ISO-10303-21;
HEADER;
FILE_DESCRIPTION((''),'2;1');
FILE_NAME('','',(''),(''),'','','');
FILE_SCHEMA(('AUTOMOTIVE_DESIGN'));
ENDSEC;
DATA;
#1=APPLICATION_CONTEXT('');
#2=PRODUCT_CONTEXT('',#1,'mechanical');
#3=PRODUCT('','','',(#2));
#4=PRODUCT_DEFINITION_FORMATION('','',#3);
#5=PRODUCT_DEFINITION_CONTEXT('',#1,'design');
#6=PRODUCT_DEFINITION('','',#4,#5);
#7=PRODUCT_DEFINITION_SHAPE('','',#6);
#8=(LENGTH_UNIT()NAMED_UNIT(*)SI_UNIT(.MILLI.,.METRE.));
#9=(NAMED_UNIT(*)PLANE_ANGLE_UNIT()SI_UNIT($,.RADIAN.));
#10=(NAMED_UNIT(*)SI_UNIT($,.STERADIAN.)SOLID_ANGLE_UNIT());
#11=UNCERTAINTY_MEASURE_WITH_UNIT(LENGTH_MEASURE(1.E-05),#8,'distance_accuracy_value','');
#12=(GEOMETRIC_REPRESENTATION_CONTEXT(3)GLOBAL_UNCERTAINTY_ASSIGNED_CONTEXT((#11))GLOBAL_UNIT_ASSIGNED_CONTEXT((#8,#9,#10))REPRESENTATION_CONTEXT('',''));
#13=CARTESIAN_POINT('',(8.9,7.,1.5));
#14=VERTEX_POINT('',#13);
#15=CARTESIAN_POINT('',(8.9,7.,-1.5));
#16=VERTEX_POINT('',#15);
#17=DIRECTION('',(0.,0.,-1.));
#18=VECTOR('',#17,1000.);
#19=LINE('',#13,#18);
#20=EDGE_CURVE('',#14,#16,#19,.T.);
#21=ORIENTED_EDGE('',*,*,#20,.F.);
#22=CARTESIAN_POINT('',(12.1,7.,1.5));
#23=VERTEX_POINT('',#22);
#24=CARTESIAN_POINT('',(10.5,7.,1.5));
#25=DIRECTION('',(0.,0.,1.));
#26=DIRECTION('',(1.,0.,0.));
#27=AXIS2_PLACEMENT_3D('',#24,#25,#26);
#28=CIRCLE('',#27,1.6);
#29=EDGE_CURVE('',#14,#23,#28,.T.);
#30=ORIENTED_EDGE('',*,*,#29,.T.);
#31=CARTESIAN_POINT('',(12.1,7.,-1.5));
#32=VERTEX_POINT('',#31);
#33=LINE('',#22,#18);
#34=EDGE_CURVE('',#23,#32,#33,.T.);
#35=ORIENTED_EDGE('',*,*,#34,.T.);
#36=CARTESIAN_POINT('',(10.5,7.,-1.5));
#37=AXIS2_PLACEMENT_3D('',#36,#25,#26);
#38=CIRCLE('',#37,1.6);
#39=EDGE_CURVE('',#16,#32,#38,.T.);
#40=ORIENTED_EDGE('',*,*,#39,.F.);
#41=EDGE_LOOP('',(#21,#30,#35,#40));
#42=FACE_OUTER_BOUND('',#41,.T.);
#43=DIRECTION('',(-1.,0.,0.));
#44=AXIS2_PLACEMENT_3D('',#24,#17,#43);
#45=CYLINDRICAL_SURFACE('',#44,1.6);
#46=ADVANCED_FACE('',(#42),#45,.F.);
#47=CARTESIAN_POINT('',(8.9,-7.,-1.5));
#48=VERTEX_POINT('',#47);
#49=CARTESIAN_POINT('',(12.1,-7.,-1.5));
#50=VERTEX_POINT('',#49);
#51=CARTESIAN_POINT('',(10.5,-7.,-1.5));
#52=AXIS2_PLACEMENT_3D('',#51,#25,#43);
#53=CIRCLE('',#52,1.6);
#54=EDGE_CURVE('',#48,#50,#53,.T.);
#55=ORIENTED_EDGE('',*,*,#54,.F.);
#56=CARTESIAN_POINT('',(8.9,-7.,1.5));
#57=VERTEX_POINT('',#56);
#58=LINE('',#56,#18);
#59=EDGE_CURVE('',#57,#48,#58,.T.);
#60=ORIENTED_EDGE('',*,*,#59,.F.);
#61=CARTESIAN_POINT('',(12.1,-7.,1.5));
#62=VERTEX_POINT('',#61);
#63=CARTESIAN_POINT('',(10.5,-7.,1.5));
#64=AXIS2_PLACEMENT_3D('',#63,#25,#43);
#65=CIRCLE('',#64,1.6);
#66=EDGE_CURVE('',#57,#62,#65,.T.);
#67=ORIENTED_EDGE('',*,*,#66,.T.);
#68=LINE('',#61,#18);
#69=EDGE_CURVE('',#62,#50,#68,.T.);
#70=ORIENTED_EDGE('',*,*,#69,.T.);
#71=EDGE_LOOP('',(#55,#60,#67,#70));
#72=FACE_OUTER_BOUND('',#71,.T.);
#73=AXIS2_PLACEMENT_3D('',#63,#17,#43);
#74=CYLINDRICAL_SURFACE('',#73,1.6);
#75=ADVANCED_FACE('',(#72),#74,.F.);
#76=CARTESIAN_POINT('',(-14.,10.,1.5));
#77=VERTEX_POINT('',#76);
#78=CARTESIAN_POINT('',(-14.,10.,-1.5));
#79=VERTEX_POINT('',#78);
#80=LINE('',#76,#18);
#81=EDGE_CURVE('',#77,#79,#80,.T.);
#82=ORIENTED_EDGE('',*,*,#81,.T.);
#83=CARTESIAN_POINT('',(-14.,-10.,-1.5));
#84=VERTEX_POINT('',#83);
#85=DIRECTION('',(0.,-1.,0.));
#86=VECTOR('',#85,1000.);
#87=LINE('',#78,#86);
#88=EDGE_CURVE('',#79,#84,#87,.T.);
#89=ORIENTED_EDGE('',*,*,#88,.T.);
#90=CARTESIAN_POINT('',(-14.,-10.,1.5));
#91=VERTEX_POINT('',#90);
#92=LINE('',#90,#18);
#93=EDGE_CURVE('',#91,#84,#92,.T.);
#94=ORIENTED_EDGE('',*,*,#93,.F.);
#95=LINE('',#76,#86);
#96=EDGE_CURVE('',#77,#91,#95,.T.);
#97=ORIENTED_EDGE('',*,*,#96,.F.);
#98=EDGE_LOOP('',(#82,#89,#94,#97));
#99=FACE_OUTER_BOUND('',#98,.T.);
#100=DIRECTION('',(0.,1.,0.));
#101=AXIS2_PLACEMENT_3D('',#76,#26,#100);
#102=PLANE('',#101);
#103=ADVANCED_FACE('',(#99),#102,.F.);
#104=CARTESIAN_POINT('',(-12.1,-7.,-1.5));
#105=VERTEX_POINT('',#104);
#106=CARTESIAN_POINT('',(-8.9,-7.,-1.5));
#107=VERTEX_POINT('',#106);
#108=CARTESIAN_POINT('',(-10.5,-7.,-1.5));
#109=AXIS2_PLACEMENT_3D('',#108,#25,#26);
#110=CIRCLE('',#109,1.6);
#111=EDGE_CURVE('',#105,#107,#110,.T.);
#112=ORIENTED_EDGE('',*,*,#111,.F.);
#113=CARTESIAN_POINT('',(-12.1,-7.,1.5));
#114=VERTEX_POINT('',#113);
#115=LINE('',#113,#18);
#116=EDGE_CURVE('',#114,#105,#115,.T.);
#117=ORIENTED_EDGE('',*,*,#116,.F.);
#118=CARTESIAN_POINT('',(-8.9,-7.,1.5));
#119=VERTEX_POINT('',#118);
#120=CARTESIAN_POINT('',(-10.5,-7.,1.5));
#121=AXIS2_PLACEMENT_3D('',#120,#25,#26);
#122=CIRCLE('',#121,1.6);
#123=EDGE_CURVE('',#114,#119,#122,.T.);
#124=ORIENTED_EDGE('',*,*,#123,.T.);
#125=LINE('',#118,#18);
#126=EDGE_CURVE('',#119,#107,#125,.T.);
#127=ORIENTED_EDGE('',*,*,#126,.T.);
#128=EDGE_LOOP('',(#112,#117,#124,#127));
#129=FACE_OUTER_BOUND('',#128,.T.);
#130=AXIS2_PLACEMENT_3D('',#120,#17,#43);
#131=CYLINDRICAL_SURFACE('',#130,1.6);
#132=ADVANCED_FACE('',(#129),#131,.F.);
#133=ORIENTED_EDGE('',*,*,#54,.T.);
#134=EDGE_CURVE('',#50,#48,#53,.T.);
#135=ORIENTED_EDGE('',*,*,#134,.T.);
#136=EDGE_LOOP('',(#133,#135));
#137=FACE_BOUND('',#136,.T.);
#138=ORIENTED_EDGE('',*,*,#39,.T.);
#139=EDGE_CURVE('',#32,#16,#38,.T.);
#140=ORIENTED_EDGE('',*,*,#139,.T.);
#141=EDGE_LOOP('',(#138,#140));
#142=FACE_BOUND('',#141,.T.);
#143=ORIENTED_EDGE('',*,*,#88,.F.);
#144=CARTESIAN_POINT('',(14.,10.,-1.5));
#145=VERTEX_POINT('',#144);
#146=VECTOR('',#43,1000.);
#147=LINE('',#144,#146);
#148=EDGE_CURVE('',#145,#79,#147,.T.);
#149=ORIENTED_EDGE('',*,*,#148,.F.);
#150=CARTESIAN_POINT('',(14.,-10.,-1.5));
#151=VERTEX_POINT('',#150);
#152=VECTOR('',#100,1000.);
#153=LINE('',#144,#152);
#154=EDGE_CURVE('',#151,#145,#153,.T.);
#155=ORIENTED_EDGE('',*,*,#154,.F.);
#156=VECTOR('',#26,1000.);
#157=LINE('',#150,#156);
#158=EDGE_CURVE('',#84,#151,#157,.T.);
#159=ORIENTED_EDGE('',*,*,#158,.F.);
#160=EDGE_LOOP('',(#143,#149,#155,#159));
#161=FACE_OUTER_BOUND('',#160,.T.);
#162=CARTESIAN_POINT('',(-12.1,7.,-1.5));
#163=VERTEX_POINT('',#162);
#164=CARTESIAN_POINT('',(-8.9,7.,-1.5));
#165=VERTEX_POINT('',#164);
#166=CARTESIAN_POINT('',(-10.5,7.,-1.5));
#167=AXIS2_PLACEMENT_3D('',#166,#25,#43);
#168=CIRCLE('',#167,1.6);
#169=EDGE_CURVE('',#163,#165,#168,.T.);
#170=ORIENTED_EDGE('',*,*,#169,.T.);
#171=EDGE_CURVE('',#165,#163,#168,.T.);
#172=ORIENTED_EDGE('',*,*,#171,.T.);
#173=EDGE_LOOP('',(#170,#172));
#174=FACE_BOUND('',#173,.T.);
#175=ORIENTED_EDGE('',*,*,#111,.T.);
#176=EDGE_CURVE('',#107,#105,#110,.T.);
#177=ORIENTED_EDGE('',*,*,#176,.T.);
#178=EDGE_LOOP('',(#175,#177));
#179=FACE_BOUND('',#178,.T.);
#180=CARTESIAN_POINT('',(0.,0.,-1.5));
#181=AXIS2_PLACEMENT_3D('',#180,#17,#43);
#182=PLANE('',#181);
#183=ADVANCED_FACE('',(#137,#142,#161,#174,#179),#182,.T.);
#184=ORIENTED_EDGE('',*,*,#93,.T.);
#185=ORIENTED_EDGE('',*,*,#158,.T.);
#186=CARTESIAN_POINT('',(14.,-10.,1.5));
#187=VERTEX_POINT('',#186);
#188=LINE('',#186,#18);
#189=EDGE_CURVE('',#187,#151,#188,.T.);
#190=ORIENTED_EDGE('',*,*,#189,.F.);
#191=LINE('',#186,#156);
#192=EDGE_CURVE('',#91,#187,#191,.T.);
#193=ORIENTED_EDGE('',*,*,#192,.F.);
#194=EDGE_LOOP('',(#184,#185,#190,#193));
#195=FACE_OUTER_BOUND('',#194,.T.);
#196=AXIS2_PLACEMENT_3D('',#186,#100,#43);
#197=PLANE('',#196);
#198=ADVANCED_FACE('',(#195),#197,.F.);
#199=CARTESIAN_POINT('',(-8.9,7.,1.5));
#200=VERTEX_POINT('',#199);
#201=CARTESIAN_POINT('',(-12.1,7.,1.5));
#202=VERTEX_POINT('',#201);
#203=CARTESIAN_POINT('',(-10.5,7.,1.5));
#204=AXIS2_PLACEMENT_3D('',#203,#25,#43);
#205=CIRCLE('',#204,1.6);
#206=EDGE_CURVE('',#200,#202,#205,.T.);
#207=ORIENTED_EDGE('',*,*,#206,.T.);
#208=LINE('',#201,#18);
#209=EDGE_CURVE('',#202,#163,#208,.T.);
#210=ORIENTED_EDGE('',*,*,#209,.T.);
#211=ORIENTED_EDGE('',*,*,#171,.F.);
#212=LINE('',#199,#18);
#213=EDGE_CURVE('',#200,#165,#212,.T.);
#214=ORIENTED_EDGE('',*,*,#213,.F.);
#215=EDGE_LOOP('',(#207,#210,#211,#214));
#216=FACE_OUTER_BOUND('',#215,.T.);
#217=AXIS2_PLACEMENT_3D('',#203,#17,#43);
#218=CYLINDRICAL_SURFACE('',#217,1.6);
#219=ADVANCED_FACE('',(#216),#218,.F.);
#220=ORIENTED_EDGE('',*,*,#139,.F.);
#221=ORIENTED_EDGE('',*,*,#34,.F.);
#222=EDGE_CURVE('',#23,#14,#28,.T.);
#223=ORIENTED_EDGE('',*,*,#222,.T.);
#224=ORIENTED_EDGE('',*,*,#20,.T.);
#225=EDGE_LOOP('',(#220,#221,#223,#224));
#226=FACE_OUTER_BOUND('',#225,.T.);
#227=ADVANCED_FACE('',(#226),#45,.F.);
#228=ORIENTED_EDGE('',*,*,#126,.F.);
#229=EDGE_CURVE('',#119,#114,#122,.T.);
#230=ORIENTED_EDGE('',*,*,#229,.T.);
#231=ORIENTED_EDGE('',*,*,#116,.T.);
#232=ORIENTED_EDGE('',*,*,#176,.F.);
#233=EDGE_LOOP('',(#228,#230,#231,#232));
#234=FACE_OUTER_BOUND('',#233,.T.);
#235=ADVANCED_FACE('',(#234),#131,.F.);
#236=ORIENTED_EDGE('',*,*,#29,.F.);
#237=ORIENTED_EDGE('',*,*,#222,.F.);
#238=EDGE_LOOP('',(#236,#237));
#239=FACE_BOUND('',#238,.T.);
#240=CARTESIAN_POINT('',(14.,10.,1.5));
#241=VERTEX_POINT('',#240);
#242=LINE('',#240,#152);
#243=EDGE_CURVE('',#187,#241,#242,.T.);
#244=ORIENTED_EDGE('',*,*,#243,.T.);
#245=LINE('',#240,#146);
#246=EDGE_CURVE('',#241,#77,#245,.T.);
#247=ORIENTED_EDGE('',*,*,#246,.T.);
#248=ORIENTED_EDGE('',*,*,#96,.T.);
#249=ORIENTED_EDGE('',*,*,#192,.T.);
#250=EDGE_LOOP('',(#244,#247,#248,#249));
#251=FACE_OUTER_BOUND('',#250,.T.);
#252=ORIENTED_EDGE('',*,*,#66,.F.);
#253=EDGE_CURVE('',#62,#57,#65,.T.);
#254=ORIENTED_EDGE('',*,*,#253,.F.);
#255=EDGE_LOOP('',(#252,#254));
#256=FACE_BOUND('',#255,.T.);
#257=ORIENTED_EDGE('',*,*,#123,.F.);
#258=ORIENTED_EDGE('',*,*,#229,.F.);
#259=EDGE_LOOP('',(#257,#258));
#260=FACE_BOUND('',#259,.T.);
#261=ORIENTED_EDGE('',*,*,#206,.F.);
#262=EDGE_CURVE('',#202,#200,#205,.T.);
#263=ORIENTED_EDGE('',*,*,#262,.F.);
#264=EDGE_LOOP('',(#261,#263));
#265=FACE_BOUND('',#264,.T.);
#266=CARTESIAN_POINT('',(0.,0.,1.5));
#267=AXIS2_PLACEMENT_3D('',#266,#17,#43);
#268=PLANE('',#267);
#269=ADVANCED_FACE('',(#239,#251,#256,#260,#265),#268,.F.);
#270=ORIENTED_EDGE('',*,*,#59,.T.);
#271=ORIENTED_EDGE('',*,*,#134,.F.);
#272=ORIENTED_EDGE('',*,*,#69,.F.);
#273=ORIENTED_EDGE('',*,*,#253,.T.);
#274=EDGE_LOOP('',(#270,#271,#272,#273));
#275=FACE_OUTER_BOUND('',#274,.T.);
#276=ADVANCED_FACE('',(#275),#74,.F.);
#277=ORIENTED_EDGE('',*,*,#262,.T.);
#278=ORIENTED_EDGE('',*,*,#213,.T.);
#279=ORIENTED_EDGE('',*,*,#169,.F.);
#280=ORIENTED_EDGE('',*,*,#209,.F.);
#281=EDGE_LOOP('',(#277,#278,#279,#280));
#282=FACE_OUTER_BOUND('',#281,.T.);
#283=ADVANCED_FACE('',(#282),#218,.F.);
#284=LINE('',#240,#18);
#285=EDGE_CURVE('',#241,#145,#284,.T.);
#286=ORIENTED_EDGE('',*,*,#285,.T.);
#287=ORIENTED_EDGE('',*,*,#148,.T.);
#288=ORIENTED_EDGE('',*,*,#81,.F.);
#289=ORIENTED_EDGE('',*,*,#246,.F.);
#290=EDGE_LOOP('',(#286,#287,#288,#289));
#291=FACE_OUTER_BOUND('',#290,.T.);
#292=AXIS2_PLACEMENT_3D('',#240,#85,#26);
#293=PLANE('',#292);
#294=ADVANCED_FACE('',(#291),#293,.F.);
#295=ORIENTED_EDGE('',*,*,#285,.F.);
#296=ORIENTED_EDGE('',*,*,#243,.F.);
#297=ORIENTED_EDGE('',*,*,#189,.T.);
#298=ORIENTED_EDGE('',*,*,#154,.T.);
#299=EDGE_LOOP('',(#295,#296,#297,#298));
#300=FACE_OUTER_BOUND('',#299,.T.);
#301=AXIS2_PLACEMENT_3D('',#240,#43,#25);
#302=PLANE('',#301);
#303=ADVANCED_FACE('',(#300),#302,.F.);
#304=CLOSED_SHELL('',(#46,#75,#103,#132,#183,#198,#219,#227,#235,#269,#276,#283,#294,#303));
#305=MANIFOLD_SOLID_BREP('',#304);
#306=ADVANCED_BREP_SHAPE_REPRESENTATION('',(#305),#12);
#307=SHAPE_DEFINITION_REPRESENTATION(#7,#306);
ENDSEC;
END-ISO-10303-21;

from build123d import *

# Parameters (mm, degrees)
SKETCH1_W           = 28
SKETCH1_H           = 20
SKETCH1_R           = 1.6
BOSS_EXTRUDE1_DEPTH = 1.5


with BuildPart() as part:
    # Sketch1 → Boss-Extrude1 (new, symmetric)
    with BuildSketch(Plane.XY):
        Rectangle(SKETCH1_W, SKETCH1_H)
        with Locations((10.5, 7)):
            Circle(SKETCH1_R, mode=Mode.SUBTRACT)
        with Locations(Location((-10.5, 7, 0), (0, 0, 180))):
            Circle(SKETCH1_R, mode=Mode.SUBTRACT)
        with Locations(Location((10.5, -7, 0), (0, 0, 180))):
            Circle(SKETCH1_R, mode=Mode.SUBTRACT)
        with Locations((-10.5, -7)):
            Circle(SKETCH1_R, mode=Mode.SUBTRACT)
    extrude(amount=BOSS_EXTRUDE1_DEPTH, both=True)


solid = part.part
